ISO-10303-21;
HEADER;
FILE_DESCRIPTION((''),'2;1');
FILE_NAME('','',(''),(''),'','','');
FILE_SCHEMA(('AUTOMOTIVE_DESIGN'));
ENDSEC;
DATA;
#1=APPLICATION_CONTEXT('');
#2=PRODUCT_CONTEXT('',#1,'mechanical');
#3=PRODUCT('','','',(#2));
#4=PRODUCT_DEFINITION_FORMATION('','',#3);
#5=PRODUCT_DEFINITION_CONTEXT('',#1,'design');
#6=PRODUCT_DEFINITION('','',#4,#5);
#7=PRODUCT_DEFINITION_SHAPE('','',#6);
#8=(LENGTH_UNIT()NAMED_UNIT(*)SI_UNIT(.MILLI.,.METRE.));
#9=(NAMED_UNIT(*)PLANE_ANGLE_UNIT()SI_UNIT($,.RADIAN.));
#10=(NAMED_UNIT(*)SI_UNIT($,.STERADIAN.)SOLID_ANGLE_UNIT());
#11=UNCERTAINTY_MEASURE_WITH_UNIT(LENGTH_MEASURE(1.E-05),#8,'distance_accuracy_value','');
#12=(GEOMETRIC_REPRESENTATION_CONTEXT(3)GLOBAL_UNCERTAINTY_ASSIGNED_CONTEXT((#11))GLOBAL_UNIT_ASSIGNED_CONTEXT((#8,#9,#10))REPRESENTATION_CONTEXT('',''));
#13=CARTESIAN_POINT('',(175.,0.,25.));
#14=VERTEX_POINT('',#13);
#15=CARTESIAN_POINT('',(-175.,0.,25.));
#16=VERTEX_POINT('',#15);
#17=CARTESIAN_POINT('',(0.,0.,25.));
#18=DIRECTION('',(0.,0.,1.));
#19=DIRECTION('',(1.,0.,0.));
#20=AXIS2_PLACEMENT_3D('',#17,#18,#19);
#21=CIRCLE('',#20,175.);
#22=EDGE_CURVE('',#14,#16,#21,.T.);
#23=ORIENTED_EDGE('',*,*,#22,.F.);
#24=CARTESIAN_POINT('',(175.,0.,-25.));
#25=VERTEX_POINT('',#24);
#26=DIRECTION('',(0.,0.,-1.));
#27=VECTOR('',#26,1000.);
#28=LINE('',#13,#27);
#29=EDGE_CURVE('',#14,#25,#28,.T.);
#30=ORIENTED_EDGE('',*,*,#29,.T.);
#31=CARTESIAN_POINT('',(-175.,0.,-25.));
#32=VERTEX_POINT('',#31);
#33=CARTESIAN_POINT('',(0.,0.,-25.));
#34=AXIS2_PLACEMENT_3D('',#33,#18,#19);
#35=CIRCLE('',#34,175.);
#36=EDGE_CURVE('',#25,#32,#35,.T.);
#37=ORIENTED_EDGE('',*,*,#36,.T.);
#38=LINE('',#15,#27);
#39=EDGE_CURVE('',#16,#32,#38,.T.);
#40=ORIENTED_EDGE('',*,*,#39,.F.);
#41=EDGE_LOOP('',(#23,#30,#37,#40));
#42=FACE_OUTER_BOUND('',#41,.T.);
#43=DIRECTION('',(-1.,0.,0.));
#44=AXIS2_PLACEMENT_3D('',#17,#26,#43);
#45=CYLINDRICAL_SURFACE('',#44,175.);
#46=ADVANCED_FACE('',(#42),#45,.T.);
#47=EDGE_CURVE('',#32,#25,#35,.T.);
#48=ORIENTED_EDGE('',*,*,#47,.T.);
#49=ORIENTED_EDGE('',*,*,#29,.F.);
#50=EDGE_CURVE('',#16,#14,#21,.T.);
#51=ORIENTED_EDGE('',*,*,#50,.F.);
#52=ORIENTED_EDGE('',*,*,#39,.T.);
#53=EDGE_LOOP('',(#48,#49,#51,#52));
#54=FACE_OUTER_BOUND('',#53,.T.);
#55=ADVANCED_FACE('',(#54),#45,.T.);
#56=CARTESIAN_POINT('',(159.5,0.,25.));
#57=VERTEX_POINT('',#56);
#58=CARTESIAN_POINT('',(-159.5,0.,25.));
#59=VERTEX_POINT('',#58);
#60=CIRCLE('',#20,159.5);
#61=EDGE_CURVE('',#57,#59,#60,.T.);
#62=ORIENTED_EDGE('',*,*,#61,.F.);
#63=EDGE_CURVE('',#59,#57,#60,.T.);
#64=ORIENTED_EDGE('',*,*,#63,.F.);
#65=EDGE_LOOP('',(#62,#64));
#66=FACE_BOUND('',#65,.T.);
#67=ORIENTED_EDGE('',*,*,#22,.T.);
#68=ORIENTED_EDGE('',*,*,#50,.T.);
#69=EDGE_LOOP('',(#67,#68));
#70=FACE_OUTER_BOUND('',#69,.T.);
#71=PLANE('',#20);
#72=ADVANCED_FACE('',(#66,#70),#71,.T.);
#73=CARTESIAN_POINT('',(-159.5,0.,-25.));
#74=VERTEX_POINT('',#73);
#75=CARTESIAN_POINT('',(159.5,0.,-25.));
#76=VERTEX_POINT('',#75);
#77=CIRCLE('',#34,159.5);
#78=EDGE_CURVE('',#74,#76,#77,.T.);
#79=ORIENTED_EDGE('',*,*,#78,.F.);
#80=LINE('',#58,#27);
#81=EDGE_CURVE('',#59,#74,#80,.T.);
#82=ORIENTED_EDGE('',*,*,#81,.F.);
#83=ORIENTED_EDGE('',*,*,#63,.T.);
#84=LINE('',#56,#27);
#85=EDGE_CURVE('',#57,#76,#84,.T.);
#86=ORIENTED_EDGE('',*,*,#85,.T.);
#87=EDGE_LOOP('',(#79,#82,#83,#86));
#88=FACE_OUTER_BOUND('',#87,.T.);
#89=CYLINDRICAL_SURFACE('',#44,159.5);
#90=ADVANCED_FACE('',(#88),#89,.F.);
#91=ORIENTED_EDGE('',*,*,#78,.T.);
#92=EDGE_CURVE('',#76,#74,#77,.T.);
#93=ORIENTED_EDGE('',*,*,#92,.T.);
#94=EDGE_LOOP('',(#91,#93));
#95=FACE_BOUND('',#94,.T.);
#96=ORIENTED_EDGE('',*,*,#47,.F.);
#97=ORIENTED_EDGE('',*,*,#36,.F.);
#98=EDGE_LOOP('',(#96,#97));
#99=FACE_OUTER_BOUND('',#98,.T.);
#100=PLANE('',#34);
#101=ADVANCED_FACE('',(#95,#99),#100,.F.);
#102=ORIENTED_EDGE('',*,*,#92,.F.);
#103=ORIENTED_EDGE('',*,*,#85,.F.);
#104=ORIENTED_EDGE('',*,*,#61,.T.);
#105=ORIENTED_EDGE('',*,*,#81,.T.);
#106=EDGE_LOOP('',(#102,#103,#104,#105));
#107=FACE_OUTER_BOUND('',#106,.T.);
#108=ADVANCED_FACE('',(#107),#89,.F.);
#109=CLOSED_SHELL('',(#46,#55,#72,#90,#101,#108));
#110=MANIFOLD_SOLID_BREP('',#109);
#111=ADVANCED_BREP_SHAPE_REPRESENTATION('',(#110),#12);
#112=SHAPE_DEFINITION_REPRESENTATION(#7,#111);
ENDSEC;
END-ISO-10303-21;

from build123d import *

# Parameters (mm, degrees)
SKETCH1_R           = 175
SKETCH1_R_2         = 159.5
BOSS_EXTRUDE1_DEPTH = 25


with BuildPart() as part:
    # Sketch1 → Boss-Extrude1 (new, symmetric)
    with BuildSketch(Plane.XY):
        Circle(SKETCH1_R)
        Circle(SKETCH1_R_2, mode=Mode.SUBTRACT)
    extrude(amount=BOSS_EXTRUDE1_DEPTH, both=True)


solid = part.part
